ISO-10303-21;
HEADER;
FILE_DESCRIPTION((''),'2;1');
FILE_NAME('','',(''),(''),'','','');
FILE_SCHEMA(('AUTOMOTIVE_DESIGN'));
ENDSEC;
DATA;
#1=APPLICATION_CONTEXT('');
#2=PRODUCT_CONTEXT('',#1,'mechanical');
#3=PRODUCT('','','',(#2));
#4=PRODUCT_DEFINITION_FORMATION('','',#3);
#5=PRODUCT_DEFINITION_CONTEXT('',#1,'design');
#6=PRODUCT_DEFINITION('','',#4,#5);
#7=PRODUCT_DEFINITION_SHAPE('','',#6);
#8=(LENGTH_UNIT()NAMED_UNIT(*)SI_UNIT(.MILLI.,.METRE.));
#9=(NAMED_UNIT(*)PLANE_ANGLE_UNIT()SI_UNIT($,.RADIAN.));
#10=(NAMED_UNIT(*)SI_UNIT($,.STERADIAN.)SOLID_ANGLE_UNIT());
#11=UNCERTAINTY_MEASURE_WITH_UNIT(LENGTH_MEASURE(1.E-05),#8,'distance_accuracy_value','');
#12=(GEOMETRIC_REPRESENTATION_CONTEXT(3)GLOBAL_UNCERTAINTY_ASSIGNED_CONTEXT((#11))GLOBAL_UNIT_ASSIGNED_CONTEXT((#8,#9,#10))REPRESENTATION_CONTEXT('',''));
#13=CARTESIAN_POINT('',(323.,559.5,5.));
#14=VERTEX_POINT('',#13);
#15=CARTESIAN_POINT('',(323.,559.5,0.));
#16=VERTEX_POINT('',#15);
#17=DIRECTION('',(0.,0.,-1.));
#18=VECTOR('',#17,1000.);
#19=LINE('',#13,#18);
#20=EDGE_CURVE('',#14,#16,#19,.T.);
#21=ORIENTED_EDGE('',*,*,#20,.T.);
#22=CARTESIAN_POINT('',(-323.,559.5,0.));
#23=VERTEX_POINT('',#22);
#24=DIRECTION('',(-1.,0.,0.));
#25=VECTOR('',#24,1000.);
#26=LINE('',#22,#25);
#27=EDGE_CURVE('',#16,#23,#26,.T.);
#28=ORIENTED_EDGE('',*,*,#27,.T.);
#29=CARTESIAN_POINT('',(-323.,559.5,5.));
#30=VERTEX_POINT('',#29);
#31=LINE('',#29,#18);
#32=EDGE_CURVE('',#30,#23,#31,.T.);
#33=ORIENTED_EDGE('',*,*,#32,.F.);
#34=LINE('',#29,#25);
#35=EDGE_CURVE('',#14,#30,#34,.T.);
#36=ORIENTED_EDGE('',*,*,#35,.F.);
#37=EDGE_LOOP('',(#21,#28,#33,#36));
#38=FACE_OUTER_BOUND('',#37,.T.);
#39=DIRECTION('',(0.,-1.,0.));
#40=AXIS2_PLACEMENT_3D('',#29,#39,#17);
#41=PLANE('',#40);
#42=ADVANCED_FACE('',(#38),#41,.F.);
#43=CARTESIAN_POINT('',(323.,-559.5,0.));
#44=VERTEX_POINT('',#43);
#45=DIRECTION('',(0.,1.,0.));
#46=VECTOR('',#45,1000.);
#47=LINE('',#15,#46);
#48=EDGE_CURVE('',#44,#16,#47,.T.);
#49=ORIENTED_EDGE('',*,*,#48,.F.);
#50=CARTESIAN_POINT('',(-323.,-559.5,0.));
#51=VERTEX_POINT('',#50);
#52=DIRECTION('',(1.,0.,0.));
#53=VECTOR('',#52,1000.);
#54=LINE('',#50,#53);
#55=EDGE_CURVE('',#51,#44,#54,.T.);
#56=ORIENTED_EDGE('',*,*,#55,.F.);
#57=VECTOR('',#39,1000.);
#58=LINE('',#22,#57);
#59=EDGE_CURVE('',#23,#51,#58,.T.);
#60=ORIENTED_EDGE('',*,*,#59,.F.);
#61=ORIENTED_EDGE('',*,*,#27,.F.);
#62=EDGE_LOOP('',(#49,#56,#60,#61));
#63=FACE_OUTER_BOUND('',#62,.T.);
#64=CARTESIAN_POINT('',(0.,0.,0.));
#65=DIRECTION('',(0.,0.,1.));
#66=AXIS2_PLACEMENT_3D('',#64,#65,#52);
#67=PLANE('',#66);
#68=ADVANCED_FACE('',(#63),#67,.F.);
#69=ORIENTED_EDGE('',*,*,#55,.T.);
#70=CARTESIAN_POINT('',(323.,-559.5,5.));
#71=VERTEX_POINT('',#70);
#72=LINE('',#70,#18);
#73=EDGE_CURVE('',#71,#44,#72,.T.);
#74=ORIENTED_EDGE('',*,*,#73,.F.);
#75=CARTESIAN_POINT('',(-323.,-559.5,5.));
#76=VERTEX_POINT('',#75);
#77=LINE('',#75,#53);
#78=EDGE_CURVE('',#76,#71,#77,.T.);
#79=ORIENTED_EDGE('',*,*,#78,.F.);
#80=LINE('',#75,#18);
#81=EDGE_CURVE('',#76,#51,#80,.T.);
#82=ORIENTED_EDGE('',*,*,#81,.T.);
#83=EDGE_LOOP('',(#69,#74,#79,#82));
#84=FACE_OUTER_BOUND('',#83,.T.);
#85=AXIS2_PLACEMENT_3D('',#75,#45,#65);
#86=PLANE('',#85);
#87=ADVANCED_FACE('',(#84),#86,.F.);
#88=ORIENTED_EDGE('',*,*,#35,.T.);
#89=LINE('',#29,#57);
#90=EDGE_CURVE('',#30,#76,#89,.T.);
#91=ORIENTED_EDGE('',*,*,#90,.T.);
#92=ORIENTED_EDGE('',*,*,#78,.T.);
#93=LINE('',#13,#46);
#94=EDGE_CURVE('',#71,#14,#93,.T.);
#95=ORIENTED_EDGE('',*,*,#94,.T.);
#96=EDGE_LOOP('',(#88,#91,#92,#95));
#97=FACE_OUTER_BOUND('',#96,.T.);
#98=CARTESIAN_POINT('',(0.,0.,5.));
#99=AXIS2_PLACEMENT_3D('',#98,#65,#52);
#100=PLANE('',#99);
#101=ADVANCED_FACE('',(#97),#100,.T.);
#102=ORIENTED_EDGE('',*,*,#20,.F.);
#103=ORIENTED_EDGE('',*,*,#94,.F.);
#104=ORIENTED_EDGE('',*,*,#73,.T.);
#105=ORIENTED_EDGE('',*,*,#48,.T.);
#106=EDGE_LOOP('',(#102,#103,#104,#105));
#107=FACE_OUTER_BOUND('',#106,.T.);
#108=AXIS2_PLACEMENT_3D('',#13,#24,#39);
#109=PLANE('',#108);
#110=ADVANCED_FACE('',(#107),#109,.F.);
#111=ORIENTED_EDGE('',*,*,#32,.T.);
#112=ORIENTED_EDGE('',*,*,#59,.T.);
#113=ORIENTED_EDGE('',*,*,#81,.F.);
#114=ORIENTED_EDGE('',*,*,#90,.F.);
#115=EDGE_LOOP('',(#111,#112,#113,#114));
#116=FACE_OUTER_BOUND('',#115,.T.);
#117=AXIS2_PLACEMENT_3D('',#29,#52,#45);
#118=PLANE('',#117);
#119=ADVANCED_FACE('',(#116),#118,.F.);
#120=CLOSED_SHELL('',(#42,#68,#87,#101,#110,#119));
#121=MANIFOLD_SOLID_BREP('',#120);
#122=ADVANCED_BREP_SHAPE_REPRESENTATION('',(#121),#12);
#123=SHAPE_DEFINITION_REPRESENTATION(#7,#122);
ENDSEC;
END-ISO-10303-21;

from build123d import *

# Parameters (mm, degrees)
SKETCH_1_W      = 646
SKETCH_1_H      = 1119
EXTRUDE_1_DEPTH = 5


with BuildPart() as part:
    # 草图1 → 凸台-拉伸1 (new body)
    with BuildSketch(Plane.XY):
        Rectangle(SKETCH_1_W, SKETCH_1_H)
    extrude(amount=EXTRUDE_1_DEPTH)


solid = part.part
